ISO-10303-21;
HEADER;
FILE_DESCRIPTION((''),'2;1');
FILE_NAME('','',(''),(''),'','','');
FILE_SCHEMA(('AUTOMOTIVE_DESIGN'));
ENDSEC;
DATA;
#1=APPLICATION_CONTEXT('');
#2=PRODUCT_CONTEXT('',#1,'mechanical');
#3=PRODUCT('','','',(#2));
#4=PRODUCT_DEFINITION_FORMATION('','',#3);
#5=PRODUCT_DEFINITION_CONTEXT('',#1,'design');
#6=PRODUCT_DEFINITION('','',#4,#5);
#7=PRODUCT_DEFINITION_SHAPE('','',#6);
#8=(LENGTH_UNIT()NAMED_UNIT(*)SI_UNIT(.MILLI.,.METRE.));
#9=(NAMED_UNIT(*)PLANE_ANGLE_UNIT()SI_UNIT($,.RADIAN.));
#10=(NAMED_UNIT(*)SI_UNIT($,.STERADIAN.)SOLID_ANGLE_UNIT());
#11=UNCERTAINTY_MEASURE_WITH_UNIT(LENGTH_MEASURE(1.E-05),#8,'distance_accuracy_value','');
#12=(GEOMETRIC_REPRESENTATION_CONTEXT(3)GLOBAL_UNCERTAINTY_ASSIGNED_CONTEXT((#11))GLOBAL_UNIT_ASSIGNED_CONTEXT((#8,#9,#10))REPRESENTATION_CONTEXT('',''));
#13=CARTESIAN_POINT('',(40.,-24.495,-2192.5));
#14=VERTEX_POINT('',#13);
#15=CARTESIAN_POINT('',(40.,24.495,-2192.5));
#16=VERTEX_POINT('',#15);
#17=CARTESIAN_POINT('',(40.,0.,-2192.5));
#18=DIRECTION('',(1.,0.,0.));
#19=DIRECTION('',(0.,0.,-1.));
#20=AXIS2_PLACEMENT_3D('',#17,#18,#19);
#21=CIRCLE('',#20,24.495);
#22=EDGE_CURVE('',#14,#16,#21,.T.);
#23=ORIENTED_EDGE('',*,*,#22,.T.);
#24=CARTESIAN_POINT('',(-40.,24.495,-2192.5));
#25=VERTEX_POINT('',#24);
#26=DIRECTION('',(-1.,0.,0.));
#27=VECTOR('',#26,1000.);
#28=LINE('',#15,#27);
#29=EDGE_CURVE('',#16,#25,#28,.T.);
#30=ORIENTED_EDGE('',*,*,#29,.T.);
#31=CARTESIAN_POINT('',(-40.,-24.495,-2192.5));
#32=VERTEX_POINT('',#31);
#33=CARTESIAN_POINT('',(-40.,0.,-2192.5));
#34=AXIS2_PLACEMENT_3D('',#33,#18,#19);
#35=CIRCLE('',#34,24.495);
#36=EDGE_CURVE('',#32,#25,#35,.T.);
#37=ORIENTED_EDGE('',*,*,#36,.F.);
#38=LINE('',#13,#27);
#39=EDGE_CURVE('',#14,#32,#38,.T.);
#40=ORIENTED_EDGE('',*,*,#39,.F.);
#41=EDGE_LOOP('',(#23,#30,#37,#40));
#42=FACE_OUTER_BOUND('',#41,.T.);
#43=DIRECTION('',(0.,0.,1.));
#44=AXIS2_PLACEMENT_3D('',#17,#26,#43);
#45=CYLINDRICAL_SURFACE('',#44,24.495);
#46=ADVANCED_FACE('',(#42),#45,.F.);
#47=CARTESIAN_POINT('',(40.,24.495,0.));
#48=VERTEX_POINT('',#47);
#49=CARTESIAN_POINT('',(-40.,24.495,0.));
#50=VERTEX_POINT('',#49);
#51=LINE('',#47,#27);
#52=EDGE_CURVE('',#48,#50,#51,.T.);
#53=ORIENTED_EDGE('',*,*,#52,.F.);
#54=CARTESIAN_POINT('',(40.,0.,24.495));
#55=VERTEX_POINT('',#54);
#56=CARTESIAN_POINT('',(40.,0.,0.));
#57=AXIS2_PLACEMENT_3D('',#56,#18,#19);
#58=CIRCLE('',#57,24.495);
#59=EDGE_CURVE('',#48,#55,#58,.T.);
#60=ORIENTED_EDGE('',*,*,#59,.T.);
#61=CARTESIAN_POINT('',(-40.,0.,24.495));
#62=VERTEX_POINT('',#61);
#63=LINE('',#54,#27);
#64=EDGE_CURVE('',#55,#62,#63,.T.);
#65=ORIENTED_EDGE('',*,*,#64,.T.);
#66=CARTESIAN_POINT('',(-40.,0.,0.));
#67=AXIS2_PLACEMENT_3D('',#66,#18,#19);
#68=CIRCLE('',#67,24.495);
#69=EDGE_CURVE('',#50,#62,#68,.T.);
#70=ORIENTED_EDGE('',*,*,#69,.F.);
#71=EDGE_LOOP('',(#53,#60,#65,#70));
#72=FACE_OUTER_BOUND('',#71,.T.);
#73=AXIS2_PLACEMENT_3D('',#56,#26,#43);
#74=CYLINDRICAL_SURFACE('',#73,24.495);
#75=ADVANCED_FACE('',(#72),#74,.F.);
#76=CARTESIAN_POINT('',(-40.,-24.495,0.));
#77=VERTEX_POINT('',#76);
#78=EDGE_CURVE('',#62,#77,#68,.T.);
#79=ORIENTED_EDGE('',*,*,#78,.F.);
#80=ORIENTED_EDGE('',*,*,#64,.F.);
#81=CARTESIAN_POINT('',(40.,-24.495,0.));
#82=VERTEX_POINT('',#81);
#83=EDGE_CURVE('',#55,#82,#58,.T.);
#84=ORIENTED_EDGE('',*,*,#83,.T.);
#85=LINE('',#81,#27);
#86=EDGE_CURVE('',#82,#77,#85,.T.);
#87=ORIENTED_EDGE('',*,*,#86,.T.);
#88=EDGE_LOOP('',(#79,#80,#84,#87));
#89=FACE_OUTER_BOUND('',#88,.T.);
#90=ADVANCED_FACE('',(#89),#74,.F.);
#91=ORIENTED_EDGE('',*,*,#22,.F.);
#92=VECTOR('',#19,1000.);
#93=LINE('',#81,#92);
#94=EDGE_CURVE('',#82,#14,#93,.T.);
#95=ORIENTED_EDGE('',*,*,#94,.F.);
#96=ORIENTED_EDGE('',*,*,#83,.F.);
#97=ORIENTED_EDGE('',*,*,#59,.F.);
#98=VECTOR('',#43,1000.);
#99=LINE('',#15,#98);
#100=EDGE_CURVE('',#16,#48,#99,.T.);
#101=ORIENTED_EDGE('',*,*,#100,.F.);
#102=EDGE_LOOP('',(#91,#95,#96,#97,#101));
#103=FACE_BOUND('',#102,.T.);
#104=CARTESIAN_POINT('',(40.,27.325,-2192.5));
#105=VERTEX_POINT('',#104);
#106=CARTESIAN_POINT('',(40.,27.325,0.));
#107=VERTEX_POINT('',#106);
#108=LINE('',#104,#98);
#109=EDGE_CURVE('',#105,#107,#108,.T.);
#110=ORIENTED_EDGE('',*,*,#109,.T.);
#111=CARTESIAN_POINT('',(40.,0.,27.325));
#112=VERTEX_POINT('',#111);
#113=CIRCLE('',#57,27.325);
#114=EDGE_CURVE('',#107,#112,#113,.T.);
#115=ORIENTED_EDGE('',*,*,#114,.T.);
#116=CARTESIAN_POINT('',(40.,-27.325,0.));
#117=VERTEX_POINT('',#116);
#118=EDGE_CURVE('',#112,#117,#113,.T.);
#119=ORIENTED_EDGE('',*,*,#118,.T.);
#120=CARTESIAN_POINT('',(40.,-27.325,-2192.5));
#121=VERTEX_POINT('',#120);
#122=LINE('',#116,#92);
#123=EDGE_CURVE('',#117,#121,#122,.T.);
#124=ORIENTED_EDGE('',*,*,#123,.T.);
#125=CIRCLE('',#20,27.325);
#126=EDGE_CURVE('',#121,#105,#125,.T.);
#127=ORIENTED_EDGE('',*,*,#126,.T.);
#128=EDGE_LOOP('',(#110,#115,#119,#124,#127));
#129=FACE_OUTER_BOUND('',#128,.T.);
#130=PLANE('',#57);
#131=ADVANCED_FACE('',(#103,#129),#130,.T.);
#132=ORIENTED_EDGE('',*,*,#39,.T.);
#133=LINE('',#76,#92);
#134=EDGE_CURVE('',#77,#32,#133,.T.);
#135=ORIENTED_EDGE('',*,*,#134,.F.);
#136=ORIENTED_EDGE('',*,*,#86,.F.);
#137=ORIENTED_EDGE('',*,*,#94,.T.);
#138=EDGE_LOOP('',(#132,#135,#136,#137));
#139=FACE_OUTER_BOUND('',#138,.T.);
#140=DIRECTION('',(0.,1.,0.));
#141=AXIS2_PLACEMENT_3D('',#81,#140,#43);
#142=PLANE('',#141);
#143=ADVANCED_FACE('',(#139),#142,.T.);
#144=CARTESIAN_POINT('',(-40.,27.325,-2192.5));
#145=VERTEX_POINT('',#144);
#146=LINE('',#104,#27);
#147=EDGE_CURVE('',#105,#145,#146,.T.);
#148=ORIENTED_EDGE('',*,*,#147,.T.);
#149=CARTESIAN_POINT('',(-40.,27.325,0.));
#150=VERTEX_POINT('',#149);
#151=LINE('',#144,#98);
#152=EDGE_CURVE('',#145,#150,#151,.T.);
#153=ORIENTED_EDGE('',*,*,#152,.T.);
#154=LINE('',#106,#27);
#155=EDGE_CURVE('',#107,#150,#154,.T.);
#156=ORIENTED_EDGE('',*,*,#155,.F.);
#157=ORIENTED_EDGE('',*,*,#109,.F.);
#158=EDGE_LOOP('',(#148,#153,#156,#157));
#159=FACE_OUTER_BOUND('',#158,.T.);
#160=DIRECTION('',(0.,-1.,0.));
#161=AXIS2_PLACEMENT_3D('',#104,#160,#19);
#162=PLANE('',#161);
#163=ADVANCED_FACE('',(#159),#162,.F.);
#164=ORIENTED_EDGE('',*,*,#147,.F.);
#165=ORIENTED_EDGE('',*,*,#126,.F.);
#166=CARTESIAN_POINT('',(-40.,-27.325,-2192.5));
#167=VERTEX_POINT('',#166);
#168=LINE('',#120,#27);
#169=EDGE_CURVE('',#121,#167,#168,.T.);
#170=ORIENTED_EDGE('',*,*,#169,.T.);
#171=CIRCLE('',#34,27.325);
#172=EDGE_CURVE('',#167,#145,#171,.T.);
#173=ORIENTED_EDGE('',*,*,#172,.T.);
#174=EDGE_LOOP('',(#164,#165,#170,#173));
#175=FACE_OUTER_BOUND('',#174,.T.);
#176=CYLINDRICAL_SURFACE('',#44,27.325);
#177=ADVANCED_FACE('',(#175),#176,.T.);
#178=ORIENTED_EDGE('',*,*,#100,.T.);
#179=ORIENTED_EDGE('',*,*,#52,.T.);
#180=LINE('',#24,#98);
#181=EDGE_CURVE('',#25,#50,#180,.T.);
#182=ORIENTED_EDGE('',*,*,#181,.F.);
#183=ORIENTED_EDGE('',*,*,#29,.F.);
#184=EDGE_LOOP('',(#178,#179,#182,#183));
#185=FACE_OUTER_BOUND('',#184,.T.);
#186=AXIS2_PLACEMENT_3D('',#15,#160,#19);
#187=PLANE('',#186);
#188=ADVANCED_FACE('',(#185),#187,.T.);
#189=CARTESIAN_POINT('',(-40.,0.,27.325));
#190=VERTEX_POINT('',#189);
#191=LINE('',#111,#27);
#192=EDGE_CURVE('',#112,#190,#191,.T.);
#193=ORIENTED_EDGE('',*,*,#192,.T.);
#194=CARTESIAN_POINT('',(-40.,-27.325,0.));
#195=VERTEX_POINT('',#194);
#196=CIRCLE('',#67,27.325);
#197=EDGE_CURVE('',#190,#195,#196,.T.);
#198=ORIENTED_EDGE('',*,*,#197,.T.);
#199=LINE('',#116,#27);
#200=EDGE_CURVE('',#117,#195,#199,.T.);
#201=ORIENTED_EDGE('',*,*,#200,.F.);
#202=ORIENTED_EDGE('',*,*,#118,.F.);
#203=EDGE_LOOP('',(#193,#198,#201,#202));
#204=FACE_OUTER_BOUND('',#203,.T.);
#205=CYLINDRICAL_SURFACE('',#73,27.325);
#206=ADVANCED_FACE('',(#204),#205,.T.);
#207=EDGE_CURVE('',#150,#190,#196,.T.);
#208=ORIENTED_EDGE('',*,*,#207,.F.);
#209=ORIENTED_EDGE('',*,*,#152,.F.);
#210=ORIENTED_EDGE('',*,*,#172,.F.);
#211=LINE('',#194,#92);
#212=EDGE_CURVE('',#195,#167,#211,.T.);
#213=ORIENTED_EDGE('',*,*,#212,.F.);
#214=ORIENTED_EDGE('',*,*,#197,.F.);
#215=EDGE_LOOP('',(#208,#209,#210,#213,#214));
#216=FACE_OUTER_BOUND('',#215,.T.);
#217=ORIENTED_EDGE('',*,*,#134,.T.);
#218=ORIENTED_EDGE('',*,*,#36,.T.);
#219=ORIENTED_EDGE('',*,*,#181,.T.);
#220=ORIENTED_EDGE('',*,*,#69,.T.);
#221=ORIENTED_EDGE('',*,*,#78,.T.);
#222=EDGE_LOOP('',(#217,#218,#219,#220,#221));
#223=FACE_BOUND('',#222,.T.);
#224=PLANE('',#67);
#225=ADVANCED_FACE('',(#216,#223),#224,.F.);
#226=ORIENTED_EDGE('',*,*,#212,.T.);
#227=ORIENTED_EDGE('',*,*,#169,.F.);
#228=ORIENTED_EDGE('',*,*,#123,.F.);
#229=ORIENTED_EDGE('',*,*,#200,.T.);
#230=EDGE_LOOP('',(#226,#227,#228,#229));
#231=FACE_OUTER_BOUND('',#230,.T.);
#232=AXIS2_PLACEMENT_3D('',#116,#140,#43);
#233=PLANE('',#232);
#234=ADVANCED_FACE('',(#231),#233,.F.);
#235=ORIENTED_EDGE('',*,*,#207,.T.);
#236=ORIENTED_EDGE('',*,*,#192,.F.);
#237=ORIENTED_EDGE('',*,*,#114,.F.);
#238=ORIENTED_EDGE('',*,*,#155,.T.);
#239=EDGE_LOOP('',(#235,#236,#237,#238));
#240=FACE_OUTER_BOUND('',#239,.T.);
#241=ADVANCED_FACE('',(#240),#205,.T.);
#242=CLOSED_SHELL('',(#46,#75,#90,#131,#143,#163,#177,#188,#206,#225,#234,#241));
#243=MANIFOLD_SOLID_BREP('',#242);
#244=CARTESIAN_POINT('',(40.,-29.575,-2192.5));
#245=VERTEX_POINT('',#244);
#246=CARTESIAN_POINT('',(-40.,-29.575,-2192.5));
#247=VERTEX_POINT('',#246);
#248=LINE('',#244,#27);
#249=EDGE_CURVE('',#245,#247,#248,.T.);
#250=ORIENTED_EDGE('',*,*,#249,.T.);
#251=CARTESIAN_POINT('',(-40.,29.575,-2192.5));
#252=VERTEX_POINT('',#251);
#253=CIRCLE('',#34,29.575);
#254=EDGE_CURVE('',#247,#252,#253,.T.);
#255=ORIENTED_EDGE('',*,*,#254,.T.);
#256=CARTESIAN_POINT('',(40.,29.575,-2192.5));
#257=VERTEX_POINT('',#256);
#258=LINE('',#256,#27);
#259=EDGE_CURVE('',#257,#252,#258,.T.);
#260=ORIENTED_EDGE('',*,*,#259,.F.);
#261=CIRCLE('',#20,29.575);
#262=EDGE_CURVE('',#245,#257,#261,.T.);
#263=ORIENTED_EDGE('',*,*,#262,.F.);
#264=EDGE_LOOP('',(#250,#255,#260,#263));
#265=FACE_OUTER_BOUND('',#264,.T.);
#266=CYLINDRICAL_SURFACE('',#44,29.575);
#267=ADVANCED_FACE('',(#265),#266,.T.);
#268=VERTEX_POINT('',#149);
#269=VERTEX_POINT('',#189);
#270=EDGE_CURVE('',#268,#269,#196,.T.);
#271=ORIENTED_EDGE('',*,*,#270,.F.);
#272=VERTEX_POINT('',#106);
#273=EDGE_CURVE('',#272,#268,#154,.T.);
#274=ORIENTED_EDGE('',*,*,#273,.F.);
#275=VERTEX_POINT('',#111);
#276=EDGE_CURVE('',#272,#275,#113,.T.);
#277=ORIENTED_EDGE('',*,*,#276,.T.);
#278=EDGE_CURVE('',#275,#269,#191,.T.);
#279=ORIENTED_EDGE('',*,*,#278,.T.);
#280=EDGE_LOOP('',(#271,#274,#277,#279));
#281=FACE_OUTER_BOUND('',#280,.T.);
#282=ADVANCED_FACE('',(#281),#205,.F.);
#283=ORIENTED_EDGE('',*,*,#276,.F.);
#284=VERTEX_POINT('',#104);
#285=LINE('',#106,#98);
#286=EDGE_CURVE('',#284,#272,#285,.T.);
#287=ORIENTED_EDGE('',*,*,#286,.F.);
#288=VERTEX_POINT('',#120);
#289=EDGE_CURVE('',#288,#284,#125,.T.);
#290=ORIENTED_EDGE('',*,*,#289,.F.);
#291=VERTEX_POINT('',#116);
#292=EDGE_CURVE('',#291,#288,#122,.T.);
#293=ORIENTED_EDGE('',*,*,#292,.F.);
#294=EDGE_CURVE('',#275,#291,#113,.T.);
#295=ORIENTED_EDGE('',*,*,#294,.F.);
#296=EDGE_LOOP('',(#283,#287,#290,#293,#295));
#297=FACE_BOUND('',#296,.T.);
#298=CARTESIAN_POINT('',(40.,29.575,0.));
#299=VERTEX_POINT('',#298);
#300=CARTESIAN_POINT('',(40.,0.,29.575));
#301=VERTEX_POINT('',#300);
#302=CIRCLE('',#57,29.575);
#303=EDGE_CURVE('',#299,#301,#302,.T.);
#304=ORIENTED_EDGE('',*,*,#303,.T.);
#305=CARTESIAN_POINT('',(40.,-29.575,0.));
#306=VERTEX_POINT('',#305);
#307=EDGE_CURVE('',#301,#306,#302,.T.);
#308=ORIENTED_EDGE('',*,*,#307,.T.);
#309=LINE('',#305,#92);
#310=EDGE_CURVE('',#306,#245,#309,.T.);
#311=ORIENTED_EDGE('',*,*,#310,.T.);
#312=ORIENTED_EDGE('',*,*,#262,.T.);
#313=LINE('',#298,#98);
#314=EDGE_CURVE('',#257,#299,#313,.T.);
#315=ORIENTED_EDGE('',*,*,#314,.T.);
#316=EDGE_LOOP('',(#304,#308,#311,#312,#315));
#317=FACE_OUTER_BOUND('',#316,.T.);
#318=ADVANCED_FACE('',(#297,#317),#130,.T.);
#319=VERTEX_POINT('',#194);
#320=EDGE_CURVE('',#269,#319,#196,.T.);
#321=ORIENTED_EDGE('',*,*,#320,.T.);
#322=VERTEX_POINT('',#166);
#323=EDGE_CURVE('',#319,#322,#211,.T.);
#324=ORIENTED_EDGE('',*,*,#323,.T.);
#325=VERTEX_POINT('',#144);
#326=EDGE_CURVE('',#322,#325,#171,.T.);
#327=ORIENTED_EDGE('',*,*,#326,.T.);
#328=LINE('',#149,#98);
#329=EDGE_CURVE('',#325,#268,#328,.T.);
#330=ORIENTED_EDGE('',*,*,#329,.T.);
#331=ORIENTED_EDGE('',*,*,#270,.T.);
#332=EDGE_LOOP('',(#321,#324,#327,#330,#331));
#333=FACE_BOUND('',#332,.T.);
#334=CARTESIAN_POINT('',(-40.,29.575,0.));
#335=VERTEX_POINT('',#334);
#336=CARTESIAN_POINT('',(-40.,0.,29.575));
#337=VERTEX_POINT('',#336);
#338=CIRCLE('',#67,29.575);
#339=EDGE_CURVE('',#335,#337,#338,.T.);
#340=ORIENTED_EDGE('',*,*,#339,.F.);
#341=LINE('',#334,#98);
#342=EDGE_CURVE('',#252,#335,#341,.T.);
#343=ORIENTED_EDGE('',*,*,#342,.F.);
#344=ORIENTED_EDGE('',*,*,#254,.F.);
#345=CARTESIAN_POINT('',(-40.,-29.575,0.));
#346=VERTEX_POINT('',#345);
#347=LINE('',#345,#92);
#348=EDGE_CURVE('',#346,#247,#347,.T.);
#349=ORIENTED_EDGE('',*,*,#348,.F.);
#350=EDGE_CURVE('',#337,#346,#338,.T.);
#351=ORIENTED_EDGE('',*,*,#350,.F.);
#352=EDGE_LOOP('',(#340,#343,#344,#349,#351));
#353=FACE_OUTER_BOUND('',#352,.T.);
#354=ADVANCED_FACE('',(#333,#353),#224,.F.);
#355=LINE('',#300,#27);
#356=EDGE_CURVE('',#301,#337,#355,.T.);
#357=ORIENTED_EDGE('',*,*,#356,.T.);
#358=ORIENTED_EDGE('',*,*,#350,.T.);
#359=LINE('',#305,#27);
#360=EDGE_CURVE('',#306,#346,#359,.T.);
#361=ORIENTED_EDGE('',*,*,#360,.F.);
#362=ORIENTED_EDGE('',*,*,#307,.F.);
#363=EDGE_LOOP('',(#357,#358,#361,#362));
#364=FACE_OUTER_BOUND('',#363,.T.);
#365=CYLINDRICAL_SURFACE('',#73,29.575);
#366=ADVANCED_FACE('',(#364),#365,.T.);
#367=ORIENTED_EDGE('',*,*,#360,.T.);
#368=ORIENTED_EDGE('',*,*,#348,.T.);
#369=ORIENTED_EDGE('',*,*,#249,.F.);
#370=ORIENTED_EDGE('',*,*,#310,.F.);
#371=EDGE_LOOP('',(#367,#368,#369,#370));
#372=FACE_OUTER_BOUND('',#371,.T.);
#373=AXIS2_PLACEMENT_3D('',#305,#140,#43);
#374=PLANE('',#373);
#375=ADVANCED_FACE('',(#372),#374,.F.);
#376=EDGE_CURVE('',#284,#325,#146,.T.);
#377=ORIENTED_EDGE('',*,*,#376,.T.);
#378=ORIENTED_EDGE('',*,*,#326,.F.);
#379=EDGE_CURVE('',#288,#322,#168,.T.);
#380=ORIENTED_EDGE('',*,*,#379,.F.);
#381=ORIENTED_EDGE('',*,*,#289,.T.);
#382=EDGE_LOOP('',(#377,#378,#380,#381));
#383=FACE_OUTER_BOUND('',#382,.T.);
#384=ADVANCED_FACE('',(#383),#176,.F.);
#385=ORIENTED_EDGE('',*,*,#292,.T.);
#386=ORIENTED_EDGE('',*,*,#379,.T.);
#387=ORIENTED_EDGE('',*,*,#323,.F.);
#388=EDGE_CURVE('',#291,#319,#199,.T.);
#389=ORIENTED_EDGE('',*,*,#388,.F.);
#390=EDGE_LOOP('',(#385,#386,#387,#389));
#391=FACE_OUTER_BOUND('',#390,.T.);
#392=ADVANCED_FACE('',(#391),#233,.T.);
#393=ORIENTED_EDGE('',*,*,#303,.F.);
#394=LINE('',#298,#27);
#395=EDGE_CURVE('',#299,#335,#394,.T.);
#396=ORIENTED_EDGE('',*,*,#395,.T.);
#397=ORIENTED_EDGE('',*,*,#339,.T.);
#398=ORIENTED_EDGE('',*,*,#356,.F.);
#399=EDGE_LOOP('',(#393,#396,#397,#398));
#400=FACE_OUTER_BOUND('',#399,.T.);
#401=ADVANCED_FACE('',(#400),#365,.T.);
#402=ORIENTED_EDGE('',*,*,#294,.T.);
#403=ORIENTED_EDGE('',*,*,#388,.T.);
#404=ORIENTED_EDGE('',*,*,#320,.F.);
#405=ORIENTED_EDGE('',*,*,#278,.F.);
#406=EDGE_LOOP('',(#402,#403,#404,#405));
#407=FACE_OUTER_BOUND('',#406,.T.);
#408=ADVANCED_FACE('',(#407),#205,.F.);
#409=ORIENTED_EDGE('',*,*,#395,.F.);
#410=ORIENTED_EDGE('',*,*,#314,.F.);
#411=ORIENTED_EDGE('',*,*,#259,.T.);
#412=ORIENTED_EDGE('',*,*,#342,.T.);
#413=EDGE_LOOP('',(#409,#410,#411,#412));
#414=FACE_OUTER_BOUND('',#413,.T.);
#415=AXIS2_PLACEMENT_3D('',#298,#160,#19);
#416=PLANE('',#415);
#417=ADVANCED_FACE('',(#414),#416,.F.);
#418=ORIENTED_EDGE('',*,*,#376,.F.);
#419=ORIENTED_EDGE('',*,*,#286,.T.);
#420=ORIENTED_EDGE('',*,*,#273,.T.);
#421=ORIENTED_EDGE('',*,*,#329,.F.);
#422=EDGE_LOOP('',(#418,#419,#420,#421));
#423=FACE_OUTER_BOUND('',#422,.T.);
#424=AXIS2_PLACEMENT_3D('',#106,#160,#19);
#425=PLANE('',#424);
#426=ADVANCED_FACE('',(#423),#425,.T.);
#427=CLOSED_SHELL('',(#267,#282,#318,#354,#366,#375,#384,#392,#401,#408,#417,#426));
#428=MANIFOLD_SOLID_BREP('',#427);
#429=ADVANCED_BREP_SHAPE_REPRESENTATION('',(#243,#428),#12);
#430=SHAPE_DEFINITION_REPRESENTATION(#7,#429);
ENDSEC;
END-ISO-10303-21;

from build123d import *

# Parameters (mm, degrees)
EXTRUDE_1_DEPTH = 40
EXTRUDE_2_DEPTH = 40


with BuildPart() as part:
    # 草图1 → 拉伸-薄壁1 (new, symmetric)
    with BuildSketch(Plane(origin=(0, 0, 0), x_dir=(0, 0, -1), z_dir=(1, 0, 0))):
        with BuildLine():
            Line((2192.5, -29.575), (0, -29.575))
            ThreePointArc((0, -29.575), (-29.575, 0), (0, 29.575))
            Line((0, 29.575), (2192.5, 29.575))
            ThreePointArc((2192.5, 29.575), (2222.075, 0), (2192.5, -29.575))
        make_face()
        with BuildLine():
            Line((2192.5, -27.325), (0, -27.325))
            ThreePointArc((0, -27.325), (-27.325, 0), (0, 27.325))
            Line((0, 27.325), (2192.5, 27.325))
            ThreePointArc((2192.5, 27.325), (2219.825, 0), (2192.5, -27.325))
        make_face(mode=Mode.SUBTRACT)
    extrude(amount=EXTRUDE_1_DEPTH, both=True)


with BuildPart() as body_2:
    # 草图2 → 拉伸-薄壁2 (new, symmetric)
    with BuildSketch(Plane(origin=(0, 0, 0), x_dir=(0, 0, -1), z_dir=(1, 0, 0))):
        with BuildLine():
            Line((0, -27.325), (2192.5, -27.325))
            ThreePointArc((2192.5, -27.325), (2219.825, 0), (2192.5, 27.325))
            Line((2192.5, 27.325), (0, 27.325))
            ThreePointArc((0, 27.325), (-27.325, 0), (0, -27.325))
        make_face()
        with BuildLine():
            Line((0, -24.495), (2192.5, -24.495))
            ThreePointArc((2192.5, -24.495), (2216.995, 0), (2192.5, 24.495))
            Line((2192.5, 24.495), (0, 24.495))
            ThreePointArc((0, 24.495), (-24.495, 0), (0, -24.495))
        make_face(mode=Mode.SUBTRACT)
    extrude(amount=EXTRUDE_2_DEPTH, both=True)


solid = Compound([part.part, body_2.part])
